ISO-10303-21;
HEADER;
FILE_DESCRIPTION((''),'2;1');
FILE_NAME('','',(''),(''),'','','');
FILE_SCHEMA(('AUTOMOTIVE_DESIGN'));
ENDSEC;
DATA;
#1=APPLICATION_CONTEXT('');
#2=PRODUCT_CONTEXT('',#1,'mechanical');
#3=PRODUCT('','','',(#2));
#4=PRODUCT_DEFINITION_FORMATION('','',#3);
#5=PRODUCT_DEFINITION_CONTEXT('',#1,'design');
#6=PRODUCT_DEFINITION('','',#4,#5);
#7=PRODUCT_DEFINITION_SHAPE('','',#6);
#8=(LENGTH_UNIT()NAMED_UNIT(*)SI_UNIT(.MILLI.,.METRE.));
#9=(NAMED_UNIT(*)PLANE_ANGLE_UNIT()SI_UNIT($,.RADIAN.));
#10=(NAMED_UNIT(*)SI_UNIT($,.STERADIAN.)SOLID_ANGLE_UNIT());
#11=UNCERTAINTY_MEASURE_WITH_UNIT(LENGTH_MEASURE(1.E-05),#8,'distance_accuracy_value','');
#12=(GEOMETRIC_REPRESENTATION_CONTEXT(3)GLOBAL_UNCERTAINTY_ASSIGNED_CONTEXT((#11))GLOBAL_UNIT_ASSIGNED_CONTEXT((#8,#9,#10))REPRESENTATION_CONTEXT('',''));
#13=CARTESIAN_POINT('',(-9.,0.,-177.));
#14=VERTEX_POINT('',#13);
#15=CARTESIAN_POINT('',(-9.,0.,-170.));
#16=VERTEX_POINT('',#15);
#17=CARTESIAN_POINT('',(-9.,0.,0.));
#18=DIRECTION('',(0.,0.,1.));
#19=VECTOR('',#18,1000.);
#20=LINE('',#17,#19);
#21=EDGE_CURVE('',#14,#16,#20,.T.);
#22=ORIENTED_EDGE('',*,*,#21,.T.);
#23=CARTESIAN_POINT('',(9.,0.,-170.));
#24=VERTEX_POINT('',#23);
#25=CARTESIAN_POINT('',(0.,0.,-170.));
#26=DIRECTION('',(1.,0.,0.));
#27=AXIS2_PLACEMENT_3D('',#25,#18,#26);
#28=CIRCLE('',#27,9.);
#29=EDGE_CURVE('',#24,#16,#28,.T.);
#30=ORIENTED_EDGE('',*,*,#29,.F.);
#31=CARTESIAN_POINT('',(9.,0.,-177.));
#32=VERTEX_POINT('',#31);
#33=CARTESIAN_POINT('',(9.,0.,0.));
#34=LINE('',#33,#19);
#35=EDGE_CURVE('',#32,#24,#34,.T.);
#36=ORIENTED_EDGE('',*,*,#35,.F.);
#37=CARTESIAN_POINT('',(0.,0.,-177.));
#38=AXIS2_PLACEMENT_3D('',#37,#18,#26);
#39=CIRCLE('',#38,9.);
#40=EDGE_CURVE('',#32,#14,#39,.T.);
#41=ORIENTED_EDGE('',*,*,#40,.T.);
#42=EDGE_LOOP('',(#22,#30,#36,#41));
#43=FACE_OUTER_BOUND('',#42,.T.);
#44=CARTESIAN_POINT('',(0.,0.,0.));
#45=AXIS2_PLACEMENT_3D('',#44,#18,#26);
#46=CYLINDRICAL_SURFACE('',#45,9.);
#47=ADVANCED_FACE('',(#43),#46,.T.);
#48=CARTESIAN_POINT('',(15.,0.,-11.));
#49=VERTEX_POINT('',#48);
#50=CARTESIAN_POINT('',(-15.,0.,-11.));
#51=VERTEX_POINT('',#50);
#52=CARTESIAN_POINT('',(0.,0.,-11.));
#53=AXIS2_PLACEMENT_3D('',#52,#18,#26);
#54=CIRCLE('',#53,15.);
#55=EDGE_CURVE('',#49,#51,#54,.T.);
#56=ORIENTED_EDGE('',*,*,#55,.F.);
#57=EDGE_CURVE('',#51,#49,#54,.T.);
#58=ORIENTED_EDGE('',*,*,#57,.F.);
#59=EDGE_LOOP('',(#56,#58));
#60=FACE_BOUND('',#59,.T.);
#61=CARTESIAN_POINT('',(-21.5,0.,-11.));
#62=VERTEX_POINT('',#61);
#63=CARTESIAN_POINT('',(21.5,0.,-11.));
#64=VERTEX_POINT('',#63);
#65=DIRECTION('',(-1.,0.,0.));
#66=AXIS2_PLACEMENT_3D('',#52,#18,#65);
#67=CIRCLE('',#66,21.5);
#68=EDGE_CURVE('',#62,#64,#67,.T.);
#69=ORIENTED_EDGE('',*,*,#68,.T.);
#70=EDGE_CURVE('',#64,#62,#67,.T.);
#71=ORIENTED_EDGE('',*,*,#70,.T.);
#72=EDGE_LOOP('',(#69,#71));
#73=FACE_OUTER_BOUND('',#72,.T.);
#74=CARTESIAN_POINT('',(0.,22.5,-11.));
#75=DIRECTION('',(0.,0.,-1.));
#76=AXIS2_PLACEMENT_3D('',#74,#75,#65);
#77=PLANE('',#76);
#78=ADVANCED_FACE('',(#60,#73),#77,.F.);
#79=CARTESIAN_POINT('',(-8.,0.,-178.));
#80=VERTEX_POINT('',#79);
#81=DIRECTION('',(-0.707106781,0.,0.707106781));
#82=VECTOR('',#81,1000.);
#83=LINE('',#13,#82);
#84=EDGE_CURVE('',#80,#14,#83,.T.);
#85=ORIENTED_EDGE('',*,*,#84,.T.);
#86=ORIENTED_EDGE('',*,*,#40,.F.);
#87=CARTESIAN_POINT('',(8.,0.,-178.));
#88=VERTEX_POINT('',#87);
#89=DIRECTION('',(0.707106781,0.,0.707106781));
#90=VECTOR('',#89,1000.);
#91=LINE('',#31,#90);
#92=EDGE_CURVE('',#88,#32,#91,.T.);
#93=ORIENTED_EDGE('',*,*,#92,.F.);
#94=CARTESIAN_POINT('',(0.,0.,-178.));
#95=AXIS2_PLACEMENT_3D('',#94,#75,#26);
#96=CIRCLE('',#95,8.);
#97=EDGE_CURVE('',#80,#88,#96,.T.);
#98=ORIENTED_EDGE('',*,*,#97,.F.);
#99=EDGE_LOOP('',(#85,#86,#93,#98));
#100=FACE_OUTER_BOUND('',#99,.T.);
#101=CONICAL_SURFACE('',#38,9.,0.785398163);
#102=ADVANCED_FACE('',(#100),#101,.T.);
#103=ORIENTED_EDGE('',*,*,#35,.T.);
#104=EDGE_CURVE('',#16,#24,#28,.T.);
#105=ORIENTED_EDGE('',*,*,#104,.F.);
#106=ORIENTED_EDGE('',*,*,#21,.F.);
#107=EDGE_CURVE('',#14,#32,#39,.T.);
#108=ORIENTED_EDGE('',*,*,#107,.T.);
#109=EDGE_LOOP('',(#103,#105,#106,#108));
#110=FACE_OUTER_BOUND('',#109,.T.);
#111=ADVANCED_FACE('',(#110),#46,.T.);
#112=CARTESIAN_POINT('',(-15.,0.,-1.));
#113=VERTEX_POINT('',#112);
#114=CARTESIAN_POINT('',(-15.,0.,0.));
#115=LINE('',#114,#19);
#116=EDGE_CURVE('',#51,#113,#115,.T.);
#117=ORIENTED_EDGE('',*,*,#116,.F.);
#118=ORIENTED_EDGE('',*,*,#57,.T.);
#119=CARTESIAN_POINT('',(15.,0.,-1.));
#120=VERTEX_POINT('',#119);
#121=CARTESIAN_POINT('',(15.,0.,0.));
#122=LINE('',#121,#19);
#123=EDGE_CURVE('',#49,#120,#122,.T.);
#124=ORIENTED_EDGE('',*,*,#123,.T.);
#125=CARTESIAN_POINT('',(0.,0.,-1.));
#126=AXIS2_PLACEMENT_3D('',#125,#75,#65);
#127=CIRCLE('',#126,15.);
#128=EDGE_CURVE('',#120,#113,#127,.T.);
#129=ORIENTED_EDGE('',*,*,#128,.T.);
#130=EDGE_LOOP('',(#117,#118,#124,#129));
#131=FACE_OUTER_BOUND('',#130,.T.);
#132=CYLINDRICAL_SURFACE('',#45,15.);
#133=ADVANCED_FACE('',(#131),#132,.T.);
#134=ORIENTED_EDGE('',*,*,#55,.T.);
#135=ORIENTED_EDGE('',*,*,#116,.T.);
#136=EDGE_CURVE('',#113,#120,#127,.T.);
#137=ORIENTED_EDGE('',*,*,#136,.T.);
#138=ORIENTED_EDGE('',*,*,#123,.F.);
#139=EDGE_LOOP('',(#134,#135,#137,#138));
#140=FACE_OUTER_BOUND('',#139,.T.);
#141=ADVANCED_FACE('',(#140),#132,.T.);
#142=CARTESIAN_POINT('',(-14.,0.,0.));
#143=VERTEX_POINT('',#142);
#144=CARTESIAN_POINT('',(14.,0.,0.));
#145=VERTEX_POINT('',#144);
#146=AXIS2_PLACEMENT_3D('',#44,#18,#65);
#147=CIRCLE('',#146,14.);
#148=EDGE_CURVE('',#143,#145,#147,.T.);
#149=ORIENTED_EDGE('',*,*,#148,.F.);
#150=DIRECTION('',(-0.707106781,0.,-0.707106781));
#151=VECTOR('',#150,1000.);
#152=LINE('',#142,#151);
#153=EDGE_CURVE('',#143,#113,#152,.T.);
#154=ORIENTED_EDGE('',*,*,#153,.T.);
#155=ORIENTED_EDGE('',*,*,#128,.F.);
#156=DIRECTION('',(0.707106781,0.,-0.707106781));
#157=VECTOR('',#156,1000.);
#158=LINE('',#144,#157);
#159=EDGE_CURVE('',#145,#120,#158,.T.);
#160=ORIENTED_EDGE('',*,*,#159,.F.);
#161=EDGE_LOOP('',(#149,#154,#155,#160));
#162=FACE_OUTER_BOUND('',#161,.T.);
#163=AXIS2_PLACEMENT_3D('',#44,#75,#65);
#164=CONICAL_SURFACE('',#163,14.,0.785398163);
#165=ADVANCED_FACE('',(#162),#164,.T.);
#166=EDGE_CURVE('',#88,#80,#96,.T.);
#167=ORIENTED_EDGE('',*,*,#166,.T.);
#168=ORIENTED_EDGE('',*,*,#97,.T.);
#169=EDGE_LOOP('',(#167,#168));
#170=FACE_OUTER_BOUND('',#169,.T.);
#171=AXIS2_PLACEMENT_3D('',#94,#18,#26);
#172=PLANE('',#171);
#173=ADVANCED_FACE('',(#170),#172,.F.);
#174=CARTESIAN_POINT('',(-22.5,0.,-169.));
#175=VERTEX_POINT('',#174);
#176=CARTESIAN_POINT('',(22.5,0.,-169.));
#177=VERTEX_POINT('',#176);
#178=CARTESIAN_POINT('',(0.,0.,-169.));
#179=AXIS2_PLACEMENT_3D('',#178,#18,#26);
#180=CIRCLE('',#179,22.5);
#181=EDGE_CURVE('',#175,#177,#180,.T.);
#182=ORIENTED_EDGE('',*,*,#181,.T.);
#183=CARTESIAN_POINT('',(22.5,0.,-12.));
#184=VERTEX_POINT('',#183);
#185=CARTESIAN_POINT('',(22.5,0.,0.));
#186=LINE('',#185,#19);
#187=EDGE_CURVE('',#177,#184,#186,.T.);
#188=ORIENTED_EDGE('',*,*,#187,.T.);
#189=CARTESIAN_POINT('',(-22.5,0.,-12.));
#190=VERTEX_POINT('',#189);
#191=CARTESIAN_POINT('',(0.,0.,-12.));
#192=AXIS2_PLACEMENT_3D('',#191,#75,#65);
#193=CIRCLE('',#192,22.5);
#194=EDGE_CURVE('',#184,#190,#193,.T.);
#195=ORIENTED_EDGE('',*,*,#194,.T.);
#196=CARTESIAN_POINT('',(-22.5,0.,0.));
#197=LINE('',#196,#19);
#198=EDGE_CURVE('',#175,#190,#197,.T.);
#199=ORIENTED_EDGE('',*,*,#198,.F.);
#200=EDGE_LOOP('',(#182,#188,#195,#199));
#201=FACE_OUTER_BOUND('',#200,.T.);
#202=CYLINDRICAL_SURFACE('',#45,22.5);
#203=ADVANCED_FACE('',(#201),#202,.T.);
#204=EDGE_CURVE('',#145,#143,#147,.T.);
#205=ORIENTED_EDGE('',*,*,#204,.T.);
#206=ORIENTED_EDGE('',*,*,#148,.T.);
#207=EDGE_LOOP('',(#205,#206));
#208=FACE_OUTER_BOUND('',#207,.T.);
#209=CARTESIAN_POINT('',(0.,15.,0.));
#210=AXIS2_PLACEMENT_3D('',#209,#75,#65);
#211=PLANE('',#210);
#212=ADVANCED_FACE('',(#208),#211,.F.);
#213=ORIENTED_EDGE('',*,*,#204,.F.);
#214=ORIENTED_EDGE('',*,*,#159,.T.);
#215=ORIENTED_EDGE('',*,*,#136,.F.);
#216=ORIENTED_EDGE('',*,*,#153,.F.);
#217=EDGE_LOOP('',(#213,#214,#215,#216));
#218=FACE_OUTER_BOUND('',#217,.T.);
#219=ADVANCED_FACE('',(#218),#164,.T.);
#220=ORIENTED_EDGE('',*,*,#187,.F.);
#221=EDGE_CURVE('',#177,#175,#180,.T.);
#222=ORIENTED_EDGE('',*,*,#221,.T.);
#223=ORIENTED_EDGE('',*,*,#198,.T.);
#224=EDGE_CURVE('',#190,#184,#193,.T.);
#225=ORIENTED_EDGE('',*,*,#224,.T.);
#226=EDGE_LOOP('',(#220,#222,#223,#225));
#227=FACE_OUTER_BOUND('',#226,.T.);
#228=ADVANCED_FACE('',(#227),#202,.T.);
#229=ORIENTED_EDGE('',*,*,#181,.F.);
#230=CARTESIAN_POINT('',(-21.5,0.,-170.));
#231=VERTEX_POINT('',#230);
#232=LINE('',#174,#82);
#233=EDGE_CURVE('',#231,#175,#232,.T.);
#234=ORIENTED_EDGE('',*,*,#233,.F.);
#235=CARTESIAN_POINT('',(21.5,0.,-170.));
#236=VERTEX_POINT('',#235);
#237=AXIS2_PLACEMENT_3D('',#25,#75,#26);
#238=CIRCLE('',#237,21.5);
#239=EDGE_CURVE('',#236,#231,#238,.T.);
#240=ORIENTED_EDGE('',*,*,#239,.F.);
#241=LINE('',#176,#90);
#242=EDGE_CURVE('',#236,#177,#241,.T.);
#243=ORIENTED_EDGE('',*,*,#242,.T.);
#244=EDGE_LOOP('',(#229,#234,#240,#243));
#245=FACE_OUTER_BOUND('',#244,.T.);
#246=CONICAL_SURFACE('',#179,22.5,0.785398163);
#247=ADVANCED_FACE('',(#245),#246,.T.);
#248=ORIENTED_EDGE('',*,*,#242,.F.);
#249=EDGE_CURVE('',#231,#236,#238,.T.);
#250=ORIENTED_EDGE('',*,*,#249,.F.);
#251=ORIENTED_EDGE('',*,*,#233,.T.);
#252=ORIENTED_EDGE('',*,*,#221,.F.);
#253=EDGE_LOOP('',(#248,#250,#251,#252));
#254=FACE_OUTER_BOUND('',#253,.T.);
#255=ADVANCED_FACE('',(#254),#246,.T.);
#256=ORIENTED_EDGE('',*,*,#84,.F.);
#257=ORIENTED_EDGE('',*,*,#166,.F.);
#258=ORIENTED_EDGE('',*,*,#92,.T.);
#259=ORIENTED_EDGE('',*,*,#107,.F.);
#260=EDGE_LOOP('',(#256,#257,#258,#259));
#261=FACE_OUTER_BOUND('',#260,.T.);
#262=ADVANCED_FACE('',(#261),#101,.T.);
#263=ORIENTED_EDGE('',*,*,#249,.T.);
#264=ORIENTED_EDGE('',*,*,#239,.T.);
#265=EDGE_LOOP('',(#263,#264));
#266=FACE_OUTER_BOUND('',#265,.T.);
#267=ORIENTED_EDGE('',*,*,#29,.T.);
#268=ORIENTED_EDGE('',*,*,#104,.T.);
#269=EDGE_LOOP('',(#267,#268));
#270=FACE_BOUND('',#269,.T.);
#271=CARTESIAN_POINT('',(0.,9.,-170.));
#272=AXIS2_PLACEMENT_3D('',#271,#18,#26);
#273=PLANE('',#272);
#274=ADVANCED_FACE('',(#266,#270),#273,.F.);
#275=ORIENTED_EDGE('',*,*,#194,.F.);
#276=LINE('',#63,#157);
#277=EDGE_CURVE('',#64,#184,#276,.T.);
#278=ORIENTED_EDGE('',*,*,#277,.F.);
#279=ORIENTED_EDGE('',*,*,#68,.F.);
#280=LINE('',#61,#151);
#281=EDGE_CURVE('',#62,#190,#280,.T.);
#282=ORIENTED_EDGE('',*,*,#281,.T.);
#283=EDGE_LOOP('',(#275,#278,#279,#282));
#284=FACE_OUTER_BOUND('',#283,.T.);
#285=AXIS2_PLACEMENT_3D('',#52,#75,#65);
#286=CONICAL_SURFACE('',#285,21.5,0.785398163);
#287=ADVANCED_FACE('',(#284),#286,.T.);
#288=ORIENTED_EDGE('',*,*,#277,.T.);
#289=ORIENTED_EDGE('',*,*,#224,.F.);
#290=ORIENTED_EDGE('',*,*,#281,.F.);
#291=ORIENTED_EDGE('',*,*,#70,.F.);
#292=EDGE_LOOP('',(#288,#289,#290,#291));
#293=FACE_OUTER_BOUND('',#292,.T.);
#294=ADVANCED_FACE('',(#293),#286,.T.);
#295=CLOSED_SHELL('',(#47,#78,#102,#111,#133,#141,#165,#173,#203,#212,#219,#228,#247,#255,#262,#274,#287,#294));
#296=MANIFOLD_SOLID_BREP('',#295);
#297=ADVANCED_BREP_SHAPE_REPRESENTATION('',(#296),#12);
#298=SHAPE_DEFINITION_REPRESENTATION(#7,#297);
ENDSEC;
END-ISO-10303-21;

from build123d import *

# Parameters (mm, degrees)
CHAMFER1_SIZE = 1


with BuildPart() as part:
    # Sketch1 → Revolve1 (revolve)
    with BuildSketch(Plane(origin=(0, 0, 0), x_dir=(0, 0, -1), z_dir=(1, 0, 0)), mode=Mode.PRIVATE) as revolve1_sk:
        Polygon((178, 0), (178, 9), (170, 9), (170, 22.5), (11, 22.5), (11, 15), (0, 15), (0, 0), align=None)
    revolve(revolve1_sk.sketch.rotate(Axis((0, 0, 0), (0, 0, -1)), 90), axis=Axis((0, 0, 0), (0, 0, -1)))

    # Chamfer1
    chamfer1_edges = [part.edges().sort_by_distance(p)[0] for p in [
        (-15, 0, 0),
        (-22.5, 0, -11),
        (-22.5, 0, -170),
        (-9, 0, -178),
    ]]
    chamfer(chamfer1_edges, length=CHAMFER1_SIZE)


solid = part.part
